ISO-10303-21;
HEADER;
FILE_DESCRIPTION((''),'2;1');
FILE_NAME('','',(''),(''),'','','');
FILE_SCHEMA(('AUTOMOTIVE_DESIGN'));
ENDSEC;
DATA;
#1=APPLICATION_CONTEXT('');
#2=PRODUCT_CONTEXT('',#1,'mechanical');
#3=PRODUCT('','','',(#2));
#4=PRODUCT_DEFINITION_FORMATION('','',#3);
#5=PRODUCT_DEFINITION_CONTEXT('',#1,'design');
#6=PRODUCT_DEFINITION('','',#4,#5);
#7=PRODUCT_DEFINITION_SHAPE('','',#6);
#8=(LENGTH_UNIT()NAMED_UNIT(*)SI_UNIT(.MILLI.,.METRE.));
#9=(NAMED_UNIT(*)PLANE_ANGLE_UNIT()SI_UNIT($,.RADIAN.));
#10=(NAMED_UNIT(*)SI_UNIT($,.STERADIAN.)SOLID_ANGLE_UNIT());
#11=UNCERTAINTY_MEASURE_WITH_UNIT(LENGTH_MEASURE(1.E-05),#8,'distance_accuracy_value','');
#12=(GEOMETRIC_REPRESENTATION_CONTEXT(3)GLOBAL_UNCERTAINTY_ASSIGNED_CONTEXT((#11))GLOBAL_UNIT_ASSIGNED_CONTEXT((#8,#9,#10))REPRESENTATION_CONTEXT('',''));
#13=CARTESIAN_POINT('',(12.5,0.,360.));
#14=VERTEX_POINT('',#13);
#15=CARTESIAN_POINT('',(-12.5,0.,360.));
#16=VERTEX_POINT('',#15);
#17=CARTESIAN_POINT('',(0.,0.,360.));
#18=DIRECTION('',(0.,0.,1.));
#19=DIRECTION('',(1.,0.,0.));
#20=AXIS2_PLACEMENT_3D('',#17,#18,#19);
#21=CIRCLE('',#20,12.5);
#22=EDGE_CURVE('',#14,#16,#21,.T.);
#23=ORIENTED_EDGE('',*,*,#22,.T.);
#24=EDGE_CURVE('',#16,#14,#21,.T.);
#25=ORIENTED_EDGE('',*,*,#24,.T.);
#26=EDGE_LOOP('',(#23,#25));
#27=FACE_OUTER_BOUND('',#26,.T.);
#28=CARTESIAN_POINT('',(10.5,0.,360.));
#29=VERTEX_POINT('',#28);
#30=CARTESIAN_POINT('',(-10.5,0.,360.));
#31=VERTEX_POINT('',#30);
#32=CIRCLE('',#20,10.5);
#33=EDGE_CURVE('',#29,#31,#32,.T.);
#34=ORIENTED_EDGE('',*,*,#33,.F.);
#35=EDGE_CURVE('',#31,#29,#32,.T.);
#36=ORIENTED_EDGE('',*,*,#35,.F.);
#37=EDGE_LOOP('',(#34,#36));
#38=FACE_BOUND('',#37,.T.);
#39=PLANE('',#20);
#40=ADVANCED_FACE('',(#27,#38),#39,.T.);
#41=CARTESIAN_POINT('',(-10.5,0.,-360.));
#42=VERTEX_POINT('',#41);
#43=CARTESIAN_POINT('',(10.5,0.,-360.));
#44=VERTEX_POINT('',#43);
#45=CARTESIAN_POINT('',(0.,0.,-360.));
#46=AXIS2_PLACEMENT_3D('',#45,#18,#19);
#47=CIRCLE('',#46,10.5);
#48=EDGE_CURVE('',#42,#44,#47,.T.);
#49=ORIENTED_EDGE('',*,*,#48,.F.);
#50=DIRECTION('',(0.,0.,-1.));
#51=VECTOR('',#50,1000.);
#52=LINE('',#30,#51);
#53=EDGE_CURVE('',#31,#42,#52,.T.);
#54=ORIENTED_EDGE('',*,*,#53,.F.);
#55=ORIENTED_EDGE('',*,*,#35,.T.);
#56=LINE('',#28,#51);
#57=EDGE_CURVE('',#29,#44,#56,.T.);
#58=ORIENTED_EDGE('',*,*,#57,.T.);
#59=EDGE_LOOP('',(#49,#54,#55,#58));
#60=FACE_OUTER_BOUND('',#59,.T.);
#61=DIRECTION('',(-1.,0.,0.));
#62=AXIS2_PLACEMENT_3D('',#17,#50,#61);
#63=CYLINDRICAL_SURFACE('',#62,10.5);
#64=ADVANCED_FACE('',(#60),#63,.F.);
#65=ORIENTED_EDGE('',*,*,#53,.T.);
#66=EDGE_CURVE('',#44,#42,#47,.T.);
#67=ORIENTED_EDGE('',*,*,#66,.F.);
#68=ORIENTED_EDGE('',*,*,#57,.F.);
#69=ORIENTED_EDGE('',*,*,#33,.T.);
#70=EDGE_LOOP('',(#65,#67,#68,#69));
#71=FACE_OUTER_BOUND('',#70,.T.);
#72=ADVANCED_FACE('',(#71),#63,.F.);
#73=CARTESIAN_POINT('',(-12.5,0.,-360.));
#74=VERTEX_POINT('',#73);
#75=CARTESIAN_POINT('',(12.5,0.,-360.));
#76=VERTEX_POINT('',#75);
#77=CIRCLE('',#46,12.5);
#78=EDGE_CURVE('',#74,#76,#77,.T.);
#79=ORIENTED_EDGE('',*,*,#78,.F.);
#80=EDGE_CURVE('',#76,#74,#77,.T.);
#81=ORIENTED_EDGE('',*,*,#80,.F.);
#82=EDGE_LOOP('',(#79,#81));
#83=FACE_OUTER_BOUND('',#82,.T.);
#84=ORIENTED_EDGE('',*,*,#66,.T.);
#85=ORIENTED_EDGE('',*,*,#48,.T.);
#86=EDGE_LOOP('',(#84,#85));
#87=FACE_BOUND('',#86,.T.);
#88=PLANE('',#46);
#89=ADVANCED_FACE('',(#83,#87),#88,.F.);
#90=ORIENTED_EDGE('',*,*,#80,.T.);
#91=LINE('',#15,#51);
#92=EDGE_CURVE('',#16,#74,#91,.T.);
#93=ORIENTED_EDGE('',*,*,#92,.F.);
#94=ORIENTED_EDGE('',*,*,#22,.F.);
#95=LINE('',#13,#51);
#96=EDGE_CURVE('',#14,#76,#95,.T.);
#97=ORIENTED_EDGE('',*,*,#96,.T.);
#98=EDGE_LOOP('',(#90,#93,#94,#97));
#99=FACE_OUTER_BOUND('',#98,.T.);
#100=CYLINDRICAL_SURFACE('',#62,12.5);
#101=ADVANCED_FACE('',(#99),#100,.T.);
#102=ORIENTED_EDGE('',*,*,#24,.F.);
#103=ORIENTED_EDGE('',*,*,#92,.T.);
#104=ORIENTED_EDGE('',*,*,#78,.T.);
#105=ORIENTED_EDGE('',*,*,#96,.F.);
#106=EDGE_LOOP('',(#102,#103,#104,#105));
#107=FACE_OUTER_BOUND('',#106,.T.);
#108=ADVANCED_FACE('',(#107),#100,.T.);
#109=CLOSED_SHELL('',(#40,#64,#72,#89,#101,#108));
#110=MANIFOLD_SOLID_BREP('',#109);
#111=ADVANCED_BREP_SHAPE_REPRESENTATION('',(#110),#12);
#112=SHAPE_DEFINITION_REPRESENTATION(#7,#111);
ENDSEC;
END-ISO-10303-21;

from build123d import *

# Parameters (mm, degrees)
SKETCH_1_R      = 12.5
SKETCH_1_R_2    = 10.5
EXTRUDE_1_DEPTH = 360


with BuildPart() as part:
    # 草图1 → 凸台-拉伸1 (new, symmetric)
    with BuildSketch(Plane.XY):
        with Locations(Location((0, 0, 0), (0, 0, 180))):
            Circle(SKETCH_1_R)
        with Locations(Location((0, 0, 0), (0, 0, 180))):
            Circle(SKETCH_1_R_2, mode=Mode.SUBTRACT)
    extrude(amount=EXTRUDE_1_DEPTH, both=True)


solid = part.part
